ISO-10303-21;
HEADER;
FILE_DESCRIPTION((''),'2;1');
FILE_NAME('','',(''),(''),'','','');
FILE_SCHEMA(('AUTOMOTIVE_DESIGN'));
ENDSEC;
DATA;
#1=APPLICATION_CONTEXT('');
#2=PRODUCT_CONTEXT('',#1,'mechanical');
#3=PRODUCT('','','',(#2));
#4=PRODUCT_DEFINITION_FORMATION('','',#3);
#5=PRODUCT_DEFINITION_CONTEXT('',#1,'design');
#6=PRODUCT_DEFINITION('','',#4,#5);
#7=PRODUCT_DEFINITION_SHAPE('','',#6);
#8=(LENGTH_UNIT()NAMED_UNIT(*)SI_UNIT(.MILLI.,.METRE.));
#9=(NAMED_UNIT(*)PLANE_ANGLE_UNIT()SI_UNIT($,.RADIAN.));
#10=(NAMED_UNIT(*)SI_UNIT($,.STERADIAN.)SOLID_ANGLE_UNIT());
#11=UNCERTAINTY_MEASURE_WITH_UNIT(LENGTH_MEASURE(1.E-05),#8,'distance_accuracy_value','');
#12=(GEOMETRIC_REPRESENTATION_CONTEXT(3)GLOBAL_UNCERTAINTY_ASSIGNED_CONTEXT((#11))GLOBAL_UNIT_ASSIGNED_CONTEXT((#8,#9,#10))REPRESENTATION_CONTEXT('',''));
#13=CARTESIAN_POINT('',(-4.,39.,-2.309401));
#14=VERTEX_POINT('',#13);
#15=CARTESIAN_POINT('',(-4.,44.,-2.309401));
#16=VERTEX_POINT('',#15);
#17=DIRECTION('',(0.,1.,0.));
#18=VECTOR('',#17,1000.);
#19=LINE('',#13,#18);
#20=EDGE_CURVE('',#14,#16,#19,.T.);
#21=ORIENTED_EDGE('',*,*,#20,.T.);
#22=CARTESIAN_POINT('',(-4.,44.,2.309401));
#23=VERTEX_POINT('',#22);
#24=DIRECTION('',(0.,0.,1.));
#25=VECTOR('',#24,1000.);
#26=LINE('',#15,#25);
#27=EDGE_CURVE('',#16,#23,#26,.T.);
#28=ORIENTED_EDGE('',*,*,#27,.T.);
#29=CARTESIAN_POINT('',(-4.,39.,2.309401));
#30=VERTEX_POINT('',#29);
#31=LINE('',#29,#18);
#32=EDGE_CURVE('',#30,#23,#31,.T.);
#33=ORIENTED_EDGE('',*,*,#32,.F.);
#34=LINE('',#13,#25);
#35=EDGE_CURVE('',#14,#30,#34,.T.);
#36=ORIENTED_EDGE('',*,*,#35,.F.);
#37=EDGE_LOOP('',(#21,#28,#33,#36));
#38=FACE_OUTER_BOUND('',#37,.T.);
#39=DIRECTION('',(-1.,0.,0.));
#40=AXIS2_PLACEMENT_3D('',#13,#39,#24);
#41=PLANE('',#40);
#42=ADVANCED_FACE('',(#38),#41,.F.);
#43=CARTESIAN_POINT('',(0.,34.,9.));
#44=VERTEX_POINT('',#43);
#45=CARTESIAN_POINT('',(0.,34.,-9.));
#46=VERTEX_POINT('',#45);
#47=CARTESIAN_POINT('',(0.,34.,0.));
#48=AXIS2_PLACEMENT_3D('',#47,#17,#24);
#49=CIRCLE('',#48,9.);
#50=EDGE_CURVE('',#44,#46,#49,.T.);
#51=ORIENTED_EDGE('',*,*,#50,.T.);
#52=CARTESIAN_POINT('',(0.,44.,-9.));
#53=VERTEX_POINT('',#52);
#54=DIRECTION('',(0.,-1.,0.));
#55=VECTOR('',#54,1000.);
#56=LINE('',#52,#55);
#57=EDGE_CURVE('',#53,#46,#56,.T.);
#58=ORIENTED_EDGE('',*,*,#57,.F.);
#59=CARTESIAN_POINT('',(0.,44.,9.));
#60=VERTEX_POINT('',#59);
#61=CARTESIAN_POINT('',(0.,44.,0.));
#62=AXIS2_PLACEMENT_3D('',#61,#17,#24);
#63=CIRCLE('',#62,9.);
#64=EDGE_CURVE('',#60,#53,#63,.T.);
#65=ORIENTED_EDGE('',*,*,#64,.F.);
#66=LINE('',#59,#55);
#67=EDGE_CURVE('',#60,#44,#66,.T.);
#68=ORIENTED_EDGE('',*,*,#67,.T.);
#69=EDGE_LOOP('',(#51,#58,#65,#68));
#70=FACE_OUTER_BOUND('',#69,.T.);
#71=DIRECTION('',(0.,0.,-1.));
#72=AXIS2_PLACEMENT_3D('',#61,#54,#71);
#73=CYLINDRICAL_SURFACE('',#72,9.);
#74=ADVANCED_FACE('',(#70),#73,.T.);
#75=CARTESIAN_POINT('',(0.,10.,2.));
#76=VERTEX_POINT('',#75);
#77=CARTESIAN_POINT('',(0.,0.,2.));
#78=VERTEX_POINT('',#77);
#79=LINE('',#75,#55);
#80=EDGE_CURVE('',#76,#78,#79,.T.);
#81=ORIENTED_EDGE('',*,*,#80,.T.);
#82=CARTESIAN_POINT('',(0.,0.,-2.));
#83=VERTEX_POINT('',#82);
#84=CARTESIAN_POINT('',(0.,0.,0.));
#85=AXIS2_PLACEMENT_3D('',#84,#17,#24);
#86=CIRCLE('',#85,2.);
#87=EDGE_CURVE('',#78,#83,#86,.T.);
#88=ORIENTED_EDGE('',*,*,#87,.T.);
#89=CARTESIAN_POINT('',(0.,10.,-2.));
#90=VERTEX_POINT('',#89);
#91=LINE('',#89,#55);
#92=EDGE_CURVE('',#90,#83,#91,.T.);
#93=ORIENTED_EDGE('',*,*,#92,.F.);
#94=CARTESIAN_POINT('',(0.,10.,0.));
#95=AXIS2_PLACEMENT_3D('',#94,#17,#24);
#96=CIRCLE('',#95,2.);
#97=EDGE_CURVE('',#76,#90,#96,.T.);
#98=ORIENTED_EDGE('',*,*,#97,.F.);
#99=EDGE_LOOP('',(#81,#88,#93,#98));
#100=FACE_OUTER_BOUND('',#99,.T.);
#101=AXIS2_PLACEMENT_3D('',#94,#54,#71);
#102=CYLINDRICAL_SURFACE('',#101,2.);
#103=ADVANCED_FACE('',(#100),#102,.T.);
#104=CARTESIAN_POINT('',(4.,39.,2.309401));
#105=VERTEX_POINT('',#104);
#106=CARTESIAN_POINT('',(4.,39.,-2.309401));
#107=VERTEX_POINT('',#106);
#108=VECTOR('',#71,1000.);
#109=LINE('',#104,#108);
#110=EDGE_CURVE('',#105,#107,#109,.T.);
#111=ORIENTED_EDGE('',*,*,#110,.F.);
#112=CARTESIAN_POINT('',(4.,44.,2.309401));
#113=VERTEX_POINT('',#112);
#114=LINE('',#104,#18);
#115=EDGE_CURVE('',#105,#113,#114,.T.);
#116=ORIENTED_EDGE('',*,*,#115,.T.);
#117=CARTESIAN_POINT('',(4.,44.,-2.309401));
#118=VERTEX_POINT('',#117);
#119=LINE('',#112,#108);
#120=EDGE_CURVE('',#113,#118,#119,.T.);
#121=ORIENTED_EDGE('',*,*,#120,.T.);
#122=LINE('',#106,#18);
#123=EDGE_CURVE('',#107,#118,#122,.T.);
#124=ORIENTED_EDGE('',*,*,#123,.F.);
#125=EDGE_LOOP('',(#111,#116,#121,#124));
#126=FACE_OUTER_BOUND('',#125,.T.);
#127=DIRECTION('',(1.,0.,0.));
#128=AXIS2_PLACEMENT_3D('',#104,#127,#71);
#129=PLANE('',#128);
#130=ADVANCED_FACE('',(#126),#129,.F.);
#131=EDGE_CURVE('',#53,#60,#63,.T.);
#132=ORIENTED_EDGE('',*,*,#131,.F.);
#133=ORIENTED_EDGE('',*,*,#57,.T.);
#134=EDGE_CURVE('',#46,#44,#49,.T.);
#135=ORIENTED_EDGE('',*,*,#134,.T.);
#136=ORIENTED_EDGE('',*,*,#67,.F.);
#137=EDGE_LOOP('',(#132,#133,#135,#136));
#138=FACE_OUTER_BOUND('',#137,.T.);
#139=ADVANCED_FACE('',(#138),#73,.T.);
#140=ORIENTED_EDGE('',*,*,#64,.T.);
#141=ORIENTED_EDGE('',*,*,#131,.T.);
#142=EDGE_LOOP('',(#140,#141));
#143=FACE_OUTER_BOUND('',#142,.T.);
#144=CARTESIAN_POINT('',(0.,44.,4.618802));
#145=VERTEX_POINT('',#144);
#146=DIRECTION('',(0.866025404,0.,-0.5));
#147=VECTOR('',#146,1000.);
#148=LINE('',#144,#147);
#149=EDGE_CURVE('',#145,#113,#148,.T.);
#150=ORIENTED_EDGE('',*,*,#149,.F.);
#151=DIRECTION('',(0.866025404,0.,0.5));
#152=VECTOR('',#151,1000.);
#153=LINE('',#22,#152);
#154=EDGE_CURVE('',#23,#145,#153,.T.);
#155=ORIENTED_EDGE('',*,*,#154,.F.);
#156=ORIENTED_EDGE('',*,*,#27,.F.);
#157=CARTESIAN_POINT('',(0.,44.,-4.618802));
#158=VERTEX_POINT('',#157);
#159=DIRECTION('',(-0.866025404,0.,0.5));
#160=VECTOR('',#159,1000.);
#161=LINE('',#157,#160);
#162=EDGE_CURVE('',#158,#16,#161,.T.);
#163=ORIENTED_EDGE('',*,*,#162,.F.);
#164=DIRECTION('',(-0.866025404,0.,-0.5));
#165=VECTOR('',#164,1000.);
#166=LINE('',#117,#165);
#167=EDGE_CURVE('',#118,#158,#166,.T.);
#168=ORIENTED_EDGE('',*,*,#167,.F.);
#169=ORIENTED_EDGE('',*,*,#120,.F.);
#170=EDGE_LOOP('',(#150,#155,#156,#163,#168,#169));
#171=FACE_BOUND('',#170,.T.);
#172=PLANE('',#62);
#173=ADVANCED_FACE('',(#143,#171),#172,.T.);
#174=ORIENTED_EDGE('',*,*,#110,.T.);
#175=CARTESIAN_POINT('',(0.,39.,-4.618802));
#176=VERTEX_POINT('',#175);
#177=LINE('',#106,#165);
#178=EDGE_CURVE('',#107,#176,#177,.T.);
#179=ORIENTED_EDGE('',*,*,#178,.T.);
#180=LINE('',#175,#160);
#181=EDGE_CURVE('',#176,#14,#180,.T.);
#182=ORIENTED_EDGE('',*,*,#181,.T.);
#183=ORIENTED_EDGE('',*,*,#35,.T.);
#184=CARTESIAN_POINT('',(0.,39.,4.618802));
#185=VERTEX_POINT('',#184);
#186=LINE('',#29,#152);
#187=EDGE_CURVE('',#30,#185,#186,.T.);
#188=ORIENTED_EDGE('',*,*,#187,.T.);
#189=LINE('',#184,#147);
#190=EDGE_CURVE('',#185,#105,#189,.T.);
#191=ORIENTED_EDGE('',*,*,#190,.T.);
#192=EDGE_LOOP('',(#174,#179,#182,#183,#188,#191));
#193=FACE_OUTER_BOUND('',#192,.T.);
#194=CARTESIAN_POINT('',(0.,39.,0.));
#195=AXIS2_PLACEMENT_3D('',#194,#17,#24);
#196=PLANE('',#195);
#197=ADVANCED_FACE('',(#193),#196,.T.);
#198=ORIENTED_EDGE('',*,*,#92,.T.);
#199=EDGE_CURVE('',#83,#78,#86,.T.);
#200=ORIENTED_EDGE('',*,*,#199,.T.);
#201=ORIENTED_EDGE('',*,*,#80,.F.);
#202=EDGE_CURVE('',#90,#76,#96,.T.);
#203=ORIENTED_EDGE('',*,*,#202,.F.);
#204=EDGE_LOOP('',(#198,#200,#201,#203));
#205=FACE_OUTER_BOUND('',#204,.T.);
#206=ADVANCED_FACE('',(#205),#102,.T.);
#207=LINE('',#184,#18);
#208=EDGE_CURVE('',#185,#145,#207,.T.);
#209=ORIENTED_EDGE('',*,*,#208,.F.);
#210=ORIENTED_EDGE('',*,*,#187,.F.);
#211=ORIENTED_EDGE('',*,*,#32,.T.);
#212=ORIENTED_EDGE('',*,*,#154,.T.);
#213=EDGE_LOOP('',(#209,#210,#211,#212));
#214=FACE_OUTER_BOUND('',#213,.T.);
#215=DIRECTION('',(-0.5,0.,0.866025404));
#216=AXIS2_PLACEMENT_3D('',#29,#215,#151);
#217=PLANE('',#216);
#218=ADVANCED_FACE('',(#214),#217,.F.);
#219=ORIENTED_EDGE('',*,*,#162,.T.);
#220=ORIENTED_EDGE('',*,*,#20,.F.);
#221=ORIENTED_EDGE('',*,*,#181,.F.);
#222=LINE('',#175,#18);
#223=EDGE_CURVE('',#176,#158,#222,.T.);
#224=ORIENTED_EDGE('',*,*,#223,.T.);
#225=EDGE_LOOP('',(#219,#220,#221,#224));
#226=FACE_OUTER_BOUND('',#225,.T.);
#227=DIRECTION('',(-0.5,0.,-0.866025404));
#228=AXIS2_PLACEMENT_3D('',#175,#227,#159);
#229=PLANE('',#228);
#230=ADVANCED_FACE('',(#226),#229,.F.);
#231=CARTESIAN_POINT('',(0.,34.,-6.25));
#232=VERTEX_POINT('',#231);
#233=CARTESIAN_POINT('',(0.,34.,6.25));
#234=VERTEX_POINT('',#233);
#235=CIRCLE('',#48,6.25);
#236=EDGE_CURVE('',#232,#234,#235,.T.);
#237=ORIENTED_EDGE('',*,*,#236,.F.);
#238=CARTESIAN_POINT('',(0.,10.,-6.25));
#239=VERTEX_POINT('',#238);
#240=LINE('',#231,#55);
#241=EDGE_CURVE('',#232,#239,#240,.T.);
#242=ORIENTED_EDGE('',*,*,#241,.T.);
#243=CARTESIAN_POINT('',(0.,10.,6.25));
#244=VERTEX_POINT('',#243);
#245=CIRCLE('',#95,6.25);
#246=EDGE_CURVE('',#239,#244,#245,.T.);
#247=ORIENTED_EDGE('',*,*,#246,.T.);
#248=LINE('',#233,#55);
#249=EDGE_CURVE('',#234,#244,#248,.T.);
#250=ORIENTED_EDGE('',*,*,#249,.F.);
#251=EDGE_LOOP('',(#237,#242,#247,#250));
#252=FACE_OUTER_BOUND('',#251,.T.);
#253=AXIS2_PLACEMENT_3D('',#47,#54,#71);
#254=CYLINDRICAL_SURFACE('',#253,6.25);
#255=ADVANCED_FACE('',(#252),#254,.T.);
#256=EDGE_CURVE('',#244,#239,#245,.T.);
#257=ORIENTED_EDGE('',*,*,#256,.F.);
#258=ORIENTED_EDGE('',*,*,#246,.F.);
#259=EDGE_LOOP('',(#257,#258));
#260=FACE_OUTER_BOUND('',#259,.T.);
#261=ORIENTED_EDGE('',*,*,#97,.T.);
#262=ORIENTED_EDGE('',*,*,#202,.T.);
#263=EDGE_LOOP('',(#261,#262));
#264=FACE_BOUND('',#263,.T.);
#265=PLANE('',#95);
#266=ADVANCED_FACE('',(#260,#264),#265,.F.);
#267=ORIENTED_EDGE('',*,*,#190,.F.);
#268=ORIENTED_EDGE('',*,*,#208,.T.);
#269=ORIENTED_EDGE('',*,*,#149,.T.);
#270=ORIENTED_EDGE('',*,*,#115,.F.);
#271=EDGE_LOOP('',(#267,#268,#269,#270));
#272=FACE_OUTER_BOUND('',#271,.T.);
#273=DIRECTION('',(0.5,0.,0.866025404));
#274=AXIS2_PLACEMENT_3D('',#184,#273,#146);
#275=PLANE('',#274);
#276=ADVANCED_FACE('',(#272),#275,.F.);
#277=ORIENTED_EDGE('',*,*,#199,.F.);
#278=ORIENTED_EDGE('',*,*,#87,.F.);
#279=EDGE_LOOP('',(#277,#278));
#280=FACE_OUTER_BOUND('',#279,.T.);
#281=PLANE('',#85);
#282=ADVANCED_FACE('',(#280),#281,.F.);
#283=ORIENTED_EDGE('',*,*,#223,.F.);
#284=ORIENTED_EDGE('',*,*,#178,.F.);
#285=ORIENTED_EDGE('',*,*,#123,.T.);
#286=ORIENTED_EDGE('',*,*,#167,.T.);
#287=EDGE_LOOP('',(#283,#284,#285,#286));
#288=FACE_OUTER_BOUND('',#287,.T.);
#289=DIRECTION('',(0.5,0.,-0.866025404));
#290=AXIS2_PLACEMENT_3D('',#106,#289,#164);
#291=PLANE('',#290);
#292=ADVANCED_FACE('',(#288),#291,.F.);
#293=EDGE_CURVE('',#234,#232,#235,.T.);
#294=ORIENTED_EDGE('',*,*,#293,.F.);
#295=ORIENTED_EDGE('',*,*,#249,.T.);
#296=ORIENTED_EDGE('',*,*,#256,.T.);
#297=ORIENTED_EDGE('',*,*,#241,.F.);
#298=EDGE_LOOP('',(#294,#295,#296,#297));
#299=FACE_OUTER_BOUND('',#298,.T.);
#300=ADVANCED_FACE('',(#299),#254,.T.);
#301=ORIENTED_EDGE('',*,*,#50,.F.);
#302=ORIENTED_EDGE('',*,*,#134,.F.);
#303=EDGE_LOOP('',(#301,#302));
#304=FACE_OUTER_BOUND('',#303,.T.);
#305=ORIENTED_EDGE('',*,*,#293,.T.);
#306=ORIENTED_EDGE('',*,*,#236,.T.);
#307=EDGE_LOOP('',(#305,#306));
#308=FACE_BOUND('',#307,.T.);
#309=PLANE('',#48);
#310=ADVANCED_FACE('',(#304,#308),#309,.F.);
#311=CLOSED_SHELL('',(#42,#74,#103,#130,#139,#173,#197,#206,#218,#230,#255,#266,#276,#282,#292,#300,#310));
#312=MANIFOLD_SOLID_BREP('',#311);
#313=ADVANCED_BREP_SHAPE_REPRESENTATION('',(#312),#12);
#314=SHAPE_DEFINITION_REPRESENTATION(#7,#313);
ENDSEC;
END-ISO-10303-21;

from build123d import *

# Parameters (mm, degrees)
SKETCH1_R           = 2
BOSS_EXTRUDE1_DEPTH = 10
SKETCH2_R           = 6.25
BOSS_EXTRUDE2_DEPTH = 24
SKETCH3_R           = 9
BOSS_EXTRUDE3_DEPTH = 10
CUT_EXTRUDE1_DEPTH  = 5


with BuildPart() as part:
    # Sketch1 → Boss-Extrude1 (new body)
    with BuildSketch(Plane(origin=(0, 0, 0), x_dir=(1, 0, 0), z_dir=(0, 1, 0))):
        with Locations(Location((0, 0, 0), (0, 0, 270))):
            Circle(SKETCH1_R)
    extrude(amount=BOSS_EXTRUDE1_DEPTH)

    # Sketch2 → Boss-Extrude2 (add)
    with BuildSketch(Plane(origin=(0, 10, 0), x_dir=(1, 0, 0), z_dir=(0, 1, 0))):
        with Locations(Location((0, 0, 0), (0, 0, 270))):
            Circle(SKETCH2_R)
    extrude(amount=BOSS_EXTRUDE2_DEPTH)

    # Sketch3 → Boss-Extrude3 (add)
    with BuildSketch(Plane(origin=(0, 34, 0), x_dir=(1, 0, 0), z_dir=(0, 1, 0))):
        with Locations(Location((0, 0, 0), (0, 0, 270))):
            Circle(SKETCH3_R)
    extrude(amount=BOSS_EXTRUDE3_DEPTH)

    # Sketch4 → Cut-Extrude1 (cut)
    with BuildSketch(Plane(origin=(0, 44, 0), x_dir=(1, 0, 0), z_dir=(0, 1, 0))):
        Polygon((0, 4.618802154), (-4, 2.309401077), (-4, -2.309401077), (0, -4.618802154), (4, -2.309401077), (4, 2.309401077), align=None)
    extrude(amount=-CUT_EXTRUDE1_DEPTH, mode=Mode.SUBTRACT)


solid = part.part
